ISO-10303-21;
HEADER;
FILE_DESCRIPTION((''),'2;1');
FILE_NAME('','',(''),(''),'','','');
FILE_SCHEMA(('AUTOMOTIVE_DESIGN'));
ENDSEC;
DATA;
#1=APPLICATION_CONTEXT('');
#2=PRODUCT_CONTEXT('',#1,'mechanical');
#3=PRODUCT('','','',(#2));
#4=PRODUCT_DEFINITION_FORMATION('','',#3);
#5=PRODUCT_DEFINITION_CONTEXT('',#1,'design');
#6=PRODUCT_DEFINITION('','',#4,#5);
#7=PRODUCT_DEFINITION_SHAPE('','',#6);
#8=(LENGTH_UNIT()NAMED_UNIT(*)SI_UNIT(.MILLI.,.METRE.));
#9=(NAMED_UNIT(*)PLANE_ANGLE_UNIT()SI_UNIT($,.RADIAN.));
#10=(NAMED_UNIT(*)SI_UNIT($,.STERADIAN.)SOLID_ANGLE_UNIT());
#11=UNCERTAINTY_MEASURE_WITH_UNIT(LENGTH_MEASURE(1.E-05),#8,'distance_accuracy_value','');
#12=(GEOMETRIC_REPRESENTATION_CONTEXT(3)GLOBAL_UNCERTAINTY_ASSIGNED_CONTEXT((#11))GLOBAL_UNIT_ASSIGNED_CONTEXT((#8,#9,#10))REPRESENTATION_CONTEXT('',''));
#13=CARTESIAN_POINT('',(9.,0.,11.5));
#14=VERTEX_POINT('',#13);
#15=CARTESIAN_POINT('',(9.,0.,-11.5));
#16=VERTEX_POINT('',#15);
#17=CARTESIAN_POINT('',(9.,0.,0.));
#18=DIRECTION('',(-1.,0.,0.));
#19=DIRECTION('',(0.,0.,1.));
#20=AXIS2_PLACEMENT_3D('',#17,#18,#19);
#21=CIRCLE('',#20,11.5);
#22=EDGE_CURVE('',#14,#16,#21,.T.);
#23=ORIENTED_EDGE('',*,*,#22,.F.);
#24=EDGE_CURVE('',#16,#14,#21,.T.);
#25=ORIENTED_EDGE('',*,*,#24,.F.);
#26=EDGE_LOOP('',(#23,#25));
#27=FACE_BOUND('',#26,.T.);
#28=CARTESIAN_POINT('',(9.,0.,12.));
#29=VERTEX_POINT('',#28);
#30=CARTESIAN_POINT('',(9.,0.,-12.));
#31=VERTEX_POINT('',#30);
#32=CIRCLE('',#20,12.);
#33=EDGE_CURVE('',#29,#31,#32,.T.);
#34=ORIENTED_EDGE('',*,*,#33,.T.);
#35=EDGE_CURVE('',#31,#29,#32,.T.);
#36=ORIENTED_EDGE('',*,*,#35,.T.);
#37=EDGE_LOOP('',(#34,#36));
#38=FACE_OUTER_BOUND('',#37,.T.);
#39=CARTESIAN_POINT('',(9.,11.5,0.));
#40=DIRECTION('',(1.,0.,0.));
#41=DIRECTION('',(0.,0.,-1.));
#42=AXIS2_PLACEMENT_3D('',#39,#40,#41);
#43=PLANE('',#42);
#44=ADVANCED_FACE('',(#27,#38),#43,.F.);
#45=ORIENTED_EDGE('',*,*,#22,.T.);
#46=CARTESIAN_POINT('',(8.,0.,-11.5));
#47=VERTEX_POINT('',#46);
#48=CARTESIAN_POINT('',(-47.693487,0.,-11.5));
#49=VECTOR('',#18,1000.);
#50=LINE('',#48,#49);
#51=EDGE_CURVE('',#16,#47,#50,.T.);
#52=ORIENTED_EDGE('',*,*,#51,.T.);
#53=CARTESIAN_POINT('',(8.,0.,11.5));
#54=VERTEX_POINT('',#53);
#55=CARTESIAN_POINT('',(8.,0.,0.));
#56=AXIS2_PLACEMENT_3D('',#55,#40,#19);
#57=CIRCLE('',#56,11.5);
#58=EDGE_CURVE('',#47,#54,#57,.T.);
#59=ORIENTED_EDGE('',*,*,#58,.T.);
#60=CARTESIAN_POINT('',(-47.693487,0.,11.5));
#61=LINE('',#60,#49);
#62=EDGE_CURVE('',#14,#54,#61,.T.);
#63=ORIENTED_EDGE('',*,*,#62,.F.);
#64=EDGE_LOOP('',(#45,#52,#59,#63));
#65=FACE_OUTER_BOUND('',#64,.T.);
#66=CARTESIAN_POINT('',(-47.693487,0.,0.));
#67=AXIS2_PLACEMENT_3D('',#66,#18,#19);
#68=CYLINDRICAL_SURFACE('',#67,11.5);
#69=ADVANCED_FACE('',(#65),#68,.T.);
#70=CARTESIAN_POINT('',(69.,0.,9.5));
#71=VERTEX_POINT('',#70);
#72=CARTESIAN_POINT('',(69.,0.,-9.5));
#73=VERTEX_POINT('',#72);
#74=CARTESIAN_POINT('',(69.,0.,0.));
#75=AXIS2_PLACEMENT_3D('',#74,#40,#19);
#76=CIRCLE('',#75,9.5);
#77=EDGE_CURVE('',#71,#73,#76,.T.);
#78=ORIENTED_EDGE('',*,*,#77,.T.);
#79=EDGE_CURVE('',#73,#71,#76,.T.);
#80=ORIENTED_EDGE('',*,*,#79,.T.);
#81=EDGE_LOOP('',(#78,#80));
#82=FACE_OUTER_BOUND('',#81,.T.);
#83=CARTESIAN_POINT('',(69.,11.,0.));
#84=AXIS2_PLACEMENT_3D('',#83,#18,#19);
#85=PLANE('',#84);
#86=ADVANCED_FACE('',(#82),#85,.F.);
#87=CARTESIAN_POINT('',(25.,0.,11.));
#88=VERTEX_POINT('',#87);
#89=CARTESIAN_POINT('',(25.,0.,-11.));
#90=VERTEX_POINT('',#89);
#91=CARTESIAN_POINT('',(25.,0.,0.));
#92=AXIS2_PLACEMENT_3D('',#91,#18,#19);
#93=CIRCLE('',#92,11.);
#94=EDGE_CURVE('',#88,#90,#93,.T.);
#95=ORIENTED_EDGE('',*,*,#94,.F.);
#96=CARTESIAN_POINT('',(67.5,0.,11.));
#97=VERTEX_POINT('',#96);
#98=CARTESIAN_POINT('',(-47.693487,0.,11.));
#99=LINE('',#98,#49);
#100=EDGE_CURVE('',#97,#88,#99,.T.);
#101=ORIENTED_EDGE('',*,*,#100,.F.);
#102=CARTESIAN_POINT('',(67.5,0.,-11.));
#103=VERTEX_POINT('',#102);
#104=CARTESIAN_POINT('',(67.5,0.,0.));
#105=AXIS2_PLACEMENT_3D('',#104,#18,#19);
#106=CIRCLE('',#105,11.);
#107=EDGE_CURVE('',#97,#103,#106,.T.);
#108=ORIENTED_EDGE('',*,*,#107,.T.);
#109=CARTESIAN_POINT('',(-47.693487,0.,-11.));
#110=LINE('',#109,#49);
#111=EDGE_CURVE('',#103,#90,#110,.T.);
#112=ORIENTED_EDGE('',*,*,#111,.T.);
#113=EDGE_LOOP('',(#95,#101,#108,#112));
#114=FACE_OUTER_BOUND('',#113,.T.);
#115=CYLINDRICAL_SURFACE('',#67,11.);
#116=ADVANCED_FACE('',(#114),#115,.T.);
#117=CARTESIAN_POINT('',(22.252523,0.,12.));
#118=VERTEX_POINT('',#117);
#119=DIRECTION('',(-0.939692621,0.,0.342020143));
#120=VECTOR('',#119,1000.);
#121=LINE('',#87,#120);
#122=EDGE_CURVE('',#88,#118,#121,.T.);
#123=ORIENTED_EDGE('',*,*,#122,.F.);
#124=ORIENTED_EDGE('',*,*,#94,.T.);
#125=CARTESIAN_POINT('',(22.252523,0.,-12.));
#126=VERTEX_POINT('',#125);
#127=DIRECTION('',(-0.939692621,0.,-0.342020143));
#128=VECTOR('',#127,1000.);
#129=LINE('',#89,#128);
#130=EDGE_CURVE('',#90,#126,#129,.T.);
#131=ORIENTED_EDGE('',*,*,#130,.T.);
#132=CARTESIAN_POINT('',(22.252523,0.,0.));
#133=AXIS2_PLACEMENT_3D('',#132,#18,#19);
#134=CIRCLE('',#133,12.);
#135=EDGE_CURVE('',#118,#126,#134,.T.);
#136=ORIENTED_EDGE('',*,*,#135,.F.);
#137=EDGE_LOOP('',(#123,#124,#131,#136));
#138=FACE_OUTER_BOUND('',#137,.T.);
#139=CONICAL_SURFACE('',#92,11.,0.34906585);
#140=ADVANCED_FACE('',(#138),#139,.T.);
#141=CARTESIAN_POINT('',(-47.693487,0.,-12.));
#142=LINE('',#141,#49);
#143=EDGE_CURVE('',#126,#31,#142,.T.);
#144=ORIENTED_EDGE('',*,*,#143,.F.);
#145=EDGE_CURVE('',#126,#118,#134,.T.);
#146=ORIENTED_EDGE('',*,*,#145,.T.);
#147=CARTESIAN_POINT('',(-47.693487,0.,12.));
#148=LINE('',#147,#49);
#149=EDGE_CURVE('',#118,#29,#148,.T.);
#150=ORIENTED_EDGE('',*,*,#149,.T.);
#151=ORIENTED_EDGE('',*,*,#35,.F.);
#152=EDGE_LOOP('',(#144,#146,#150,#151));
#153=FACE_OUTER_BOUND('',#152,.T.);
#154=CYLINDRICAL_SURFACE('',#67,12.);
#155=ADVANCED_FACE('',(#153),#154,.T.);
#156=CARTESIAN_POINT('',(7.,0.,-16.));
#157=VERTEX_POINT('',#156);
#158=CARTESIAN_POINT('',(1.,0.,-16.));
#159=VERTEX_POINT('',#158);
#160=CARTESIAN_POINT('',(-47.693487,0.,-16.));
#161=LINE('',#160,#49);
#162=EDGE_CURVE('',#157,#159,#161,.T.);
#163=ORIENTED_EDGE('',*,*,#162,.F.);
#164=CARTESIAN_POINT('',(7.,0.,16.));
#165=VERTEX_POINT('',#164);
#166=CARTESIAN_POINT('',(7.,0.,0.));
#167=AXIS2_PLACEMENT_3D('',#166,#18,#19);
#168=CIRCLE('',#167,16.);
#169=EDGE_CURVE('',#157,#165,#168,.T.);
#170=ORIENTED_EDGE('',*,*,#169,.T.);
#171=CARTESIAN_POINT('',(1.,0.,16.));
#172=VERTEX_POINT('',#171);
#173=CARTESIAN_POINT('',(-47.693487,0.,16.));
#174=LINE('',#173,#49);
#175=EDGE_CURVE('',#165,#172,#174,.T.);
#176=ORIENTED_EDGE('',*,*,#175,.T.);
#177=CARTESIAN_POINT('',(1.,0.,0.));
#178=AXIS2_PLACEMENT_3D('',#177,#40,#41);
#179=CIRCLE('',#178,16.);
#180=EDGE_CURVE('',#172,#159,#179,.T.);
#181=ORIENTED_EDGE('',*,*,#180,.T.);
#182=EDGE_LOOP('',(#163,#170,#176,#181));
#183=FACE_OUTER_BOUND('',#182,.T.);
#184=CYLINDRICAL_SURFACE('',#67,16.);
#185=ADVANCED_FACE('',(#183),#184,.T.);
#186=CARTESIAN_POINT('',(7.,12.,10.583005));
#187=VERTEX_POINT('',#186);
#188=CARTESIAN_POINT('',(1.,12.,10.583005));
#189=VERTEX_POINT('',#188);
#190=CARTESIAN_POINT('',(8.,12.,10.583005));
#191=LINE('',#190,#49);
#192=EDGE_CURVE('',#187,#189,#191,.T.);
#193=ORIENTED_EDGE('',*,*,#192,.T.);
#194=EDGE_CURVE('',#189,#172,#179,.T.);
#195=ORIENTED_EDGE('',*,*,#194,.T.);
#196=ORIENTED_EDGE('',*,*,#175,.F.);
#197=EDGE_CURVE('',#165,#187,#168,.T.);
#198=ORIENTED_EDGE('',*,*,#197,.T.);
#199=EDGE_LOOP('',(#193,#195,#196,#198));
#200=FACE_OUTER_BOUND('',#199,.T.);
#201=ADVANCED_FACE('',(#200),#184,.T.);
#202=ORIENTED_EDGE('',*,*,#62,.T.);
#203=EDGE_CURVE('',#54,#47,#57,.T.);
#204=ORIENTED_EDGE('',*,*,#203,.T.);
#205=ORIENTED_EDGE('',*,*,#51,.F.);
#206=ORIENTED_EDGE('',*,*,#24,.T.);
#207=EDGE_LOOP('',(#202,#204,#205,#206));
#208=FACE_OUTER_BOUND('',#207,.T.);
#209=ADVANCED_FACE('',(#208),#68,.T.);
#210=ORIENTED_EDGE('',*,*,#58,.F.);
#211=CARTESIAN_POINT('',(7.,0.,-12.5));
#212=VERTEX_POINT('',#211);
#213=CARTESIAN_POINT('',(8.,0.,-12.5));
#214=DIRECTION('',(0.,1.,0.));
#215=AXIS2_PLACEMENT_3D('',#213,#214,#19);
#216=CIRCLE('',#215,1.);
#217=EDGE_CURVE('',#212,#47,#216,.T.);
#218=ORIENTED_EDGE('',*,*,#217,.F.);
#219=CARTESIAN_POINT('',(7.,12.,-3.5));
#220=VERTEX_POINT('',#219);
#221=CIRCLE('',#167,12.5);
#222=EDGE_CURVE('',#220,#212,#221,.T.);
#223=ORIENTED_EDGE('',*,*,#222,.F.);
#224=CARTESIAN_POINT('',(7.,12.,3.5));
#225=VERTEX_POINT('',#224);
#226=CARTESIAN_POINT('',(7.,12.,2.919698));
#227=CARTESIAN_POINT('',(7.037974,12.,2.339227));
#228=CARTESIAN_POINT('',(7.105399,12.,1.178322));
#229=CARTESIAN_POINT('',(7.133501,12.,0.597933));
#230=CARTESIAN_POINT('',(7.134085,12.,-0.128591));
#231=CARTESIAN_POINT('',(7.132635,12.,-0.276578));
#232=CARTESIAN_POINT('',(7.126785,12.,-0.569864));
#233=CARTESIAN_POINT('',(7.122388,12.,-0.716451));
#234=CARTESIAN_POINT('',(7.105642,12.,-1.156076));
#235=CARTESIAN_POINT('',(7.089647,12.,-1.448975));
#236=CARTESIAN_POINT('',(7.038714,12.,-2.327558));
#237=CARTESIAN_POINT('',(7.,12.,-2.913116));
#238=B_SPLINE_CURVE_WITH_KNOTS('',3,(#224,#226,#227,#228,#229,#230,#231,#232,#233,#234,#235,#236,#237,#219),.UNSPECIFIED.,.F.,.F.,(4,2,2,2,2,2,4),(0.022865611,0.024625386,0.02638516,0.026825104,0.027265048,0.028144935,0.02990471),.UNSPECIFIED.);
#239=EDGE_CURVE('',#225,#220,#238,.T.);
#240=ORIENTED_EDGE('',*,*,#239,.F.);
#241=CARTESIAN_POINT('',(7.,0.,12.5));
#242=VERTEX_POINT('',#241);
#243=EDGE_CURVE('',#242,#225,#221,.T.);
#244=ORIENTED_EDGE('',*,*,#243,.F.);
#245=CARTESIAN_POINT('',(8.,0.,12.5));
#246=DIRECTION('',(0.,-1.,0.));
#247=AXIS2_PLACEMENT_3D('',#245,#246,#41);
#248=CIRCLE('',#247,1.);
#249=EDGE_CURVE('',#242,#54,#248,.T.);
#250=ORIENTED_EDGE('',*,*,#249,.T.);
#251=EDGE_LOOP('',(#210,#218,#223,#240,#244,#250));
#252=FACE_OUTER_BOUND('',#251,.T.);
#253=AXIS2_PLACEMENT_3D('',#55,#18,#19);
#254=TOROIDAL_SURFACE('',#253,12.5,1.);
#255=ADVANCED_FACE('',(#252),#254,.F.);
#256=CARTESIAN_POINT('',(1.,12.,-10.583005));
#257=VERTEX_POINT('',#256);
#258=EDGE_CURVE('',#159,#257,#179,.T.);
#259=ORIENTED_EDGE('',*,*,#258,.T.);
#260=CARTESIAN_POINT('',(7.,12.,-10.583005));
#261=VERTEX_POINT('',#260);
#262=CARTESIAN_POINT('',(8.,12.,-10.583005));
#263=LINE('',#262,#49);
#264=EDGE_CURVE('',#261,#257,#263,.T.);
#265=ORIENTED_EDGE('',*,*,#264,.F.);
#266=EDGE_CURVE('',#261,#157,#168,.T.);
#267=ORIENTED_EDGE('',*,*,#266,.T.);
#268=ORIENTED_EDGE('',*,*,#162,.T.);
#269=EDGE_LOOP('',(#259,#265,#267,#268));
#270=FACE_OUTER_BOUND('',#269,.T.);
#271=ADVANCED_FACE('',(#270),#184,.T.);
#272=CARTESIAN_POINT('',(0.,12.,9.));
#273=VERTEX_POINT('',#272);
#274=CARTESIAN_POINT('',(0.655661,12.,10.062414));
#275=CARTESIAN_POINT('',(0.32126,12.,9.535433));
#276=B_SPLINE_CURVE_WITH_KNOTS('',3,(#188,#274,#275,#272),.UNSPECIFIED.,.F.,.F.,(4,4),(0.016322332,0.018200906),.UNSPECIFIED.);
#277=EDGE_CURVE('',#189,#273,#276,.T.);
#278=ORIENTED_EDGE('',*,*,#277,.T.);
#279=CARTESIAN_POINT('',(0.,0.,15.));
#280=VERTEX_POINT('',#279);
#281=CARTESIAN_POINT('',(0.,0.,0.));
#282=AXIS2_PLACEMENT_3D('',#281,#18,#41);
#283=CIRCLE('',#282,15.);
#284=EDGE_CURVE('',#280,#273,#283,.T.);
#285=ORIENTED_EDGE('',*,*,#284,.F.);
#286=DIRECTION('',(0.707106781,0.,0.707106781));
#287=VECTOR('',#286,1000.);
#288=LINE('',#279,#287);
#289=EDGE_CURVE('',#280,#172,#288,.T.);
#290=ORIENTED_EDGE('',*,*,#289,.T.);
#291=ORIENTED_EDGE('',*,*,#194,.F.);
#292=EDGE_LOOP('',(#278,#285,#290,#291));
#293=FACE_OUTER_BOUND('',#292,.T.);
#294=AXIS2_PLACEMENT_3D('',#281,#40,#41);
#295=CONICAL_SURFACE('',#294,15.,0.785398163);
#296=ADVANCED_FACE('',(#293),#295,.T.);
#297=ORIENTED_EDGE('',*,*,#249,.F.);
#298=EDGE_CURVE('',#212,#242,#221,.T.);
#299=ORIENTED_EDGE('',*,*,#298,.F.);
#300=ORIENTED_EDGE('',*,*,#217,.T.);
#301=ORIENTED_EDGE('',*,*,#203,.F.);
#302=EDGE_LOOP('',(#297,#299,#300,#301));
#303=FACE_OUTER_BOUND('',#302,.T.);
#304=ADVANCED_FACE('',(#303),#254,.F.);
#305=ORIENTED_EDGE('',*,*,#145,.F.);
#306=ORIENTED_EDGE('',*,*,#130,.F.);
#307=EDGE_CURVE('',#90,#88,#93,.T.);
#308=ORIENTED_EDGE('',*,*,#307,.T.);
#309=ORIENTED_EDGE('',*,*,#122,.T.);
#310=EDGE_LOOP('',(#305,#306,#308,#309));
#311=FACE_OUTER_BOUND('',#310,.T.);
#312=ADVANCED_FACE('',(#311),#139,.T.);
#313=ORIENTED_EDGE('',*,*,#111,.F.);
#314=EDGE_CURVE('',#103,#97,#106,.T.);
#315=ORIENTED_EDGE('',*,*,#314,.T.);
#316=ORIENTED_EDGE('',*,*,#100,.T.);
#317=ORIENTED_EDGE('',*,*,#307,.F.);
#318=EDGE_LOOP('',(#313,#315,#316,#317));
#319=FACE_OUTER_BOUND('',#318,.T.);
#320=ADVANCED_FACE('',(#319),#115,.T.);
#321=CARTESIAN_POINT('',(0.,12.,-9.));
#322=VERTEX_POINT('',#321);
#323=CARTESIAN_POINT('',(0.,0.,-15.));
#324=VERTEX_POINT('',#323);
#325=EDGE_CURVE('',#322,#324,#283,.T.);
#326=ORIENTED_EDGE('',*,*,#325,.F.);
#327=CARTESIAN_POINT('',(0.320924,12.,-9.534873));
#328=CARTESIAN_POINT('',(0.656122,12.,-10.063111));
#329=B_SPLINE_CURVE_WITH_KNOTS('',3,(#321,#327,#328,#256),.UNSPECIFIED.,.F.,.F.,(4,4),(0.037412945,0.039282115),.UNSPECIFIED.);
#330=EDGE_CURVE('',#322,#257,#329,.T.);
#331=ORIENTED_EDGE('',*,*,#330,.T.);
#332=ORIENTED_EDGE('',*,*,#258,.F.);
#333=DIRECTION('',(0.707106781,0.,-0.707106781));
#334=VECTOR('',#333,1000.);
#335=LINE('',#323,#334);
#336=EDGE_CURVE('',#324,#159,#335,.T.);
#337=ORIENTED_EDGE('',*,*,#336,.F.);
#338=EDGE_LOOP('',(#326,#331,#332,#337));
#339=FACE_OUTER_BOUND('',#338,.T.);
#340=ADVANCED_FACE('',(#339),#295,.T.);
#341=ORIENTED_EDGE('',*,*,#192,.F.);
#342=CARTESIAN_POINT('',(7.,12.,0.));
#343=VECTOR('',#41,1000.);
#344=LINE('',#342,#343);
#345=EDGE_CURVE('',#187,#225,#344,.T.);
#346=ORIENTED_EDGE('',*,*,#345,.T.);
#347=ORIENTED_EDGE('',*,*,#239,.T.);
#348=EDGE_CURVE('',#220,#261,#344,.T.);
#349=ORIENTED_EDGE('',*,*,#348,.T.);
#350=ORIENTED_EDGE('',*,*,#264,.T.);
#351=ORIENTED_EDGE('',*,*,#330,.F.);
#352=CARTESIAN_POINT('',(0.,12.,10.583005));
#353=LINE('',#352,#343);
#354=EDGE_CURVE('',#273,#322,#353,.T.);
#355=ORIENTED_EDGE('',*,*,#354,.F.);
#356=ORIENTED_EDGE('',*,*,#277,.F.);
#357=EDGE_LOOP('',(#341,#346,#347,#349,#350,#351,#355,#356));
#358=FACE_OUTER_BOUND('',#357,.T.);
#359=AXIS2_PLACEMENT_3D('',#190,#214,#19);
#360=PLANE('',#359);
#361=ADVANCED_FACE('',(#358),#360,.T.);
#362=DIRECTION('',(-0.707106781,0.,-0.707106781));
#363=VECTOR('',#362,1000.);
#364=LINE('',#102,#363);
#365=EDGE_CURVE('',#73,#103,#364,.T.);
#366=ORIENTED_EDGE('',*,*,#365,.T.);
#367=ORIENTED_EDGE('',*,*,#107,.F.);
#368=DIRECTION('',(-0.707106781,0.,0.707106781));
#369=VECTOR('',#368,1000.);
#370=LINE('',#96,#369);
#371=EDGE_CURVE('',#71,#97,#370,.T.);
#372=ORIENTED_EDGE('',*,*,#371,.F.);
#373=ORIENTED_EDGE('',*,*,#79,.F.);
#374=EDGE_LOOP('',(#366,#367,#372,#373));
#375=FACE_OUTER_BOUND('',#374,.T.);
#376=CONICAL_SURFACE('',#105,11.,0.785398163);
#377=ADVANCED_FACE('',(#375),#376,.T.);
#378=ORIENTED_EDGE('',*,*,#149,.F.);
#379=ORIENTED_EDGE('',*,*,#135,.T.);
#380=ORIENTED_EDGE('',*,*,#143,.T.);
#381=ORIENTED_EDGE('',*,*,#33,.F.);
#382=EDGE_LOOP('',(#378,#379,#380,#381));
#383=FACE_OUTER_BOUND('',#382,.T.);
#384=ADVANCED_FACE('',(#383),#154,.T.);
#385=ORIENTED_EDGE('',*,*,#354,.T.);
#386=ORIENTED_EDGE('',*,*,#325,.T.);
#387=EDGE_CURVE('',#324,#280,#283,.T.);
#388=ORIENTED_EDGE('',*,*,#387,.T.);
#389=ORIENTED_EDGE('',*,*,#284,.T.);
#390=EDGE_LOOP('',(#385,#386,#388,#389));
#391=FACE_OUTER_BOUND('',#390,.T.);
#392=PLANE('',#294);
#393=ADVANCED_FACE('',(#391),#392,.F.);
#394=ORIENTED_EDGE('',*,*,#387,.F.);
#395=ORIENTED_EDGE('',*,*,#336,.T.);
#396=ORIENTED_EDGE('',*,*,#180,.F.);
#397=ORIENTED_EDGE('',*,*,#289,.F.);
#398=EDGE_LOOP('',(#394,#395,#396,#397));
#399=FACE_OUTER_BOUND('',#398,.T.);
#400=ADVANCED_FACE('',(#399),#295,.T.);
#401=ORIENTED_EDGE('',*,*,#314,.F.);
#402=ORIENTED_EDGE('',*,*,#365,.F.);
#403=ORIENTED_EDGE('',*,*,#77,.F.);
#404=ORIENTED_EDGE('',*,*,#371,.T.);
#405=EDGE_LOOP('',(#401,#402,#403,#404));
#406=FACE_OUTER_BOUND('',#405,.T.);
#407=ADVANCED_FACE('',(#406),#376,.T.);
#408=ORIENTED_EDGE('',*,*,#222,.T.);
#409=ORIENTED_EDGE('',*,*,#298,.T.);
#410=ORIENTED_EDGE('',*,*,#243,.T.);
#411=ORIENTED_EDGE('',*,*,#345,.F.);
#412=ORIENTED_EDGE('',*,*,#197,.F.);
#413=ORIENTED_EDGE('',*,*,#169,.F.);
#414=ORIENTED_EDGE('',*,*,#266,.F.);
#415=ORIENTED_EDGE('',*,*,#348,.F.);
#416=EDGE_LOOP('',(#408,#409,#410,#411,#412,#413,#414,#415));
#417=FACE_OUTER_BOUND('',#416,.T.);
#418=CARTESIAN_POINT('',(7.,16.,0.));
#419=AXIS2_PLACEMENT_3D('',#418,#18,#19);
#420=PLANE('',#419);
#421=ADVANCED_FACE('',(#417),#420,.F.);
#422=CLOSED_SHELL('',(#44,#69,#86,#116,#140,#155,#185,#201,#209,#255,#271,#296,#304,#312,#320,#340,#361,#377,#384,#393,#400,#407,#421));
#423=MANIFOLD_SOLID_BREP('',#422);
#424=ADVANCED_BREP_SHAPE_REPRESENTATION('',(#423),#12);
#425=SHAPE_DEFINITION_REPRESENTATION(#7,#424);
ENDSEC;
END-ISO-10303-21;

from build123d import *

# Parameters (mm, degrees)
CHAMFER_1_SIZE      = 1
FILLET_1_R          = 1
CHAMFER_3_SIZE      = 1.5
CUT_EXTRUDE_START   = 8
CUT_EXTRUDE_5_DEPTH = 8


with BuildPart() as part:
    # 草图1 → 旋转1 (revolve)
    with BuildSketch(Plane.XY, mode=Mode.PRIVATE) as revolve_1_sk:
        Polygon((0, 0), (0, 16), (7, 16), (7, 11.5), (9, 11.5), (9, 12), (22.252522581, 12), (25, 11), (69, 11), (69, 0), align=None)
    revolve(revolve_1_sk.sketch.rotate(Axis((-47.69348659, 0, 0), (1, 0, 0)), 90), axis=Axis((-47.69348659, 0, 0), (1, 0, 0)))

    # 倒角1
    chamfer_1_edges = [part.edges().sort_by_distance(p)[0] for p in [
        (0, 0, -16),
    ]]
    chamfer(chamfer_1_edges, length=CHAMFER_1_SIZE)

    # 圆角1
    fillet_1_edges = [part.edges().sort_by_distance(p)[0] for p in [
        (7, 0, -11.5),
    ]]
    fillet(fillet_1_edges, radius=FILLET_1_R)

    # 倒角3
    chamfer_3_edges = [part.edges().sort_by_distance(p)[0] for p in [
        (69, 0, -11),
    ]]
    chamfer(chamfer_3_edges, length=CHAMFER_3_SIZE)

    # 草图2 → 切除-拉伸5 (cut)
    with BuildSketch(Plane(origin=(0, 0, 0), x_dir=(0, 0, -1), z_dir=(1, 0, 0)).offset(CUT_EXTRUDE_START)):
        with BuildLine():
            Line((-10.583005244, 12), (10.583005244, 12))
            ThreePointArc((10.583005244, 12), (0, 16), (-10.583005244, 12))
        make_face()
    extrude(amount=-CUT_EXTRUDE_5_DEPTH, mode=Mode.SUBTRACT)


solid = part.part
